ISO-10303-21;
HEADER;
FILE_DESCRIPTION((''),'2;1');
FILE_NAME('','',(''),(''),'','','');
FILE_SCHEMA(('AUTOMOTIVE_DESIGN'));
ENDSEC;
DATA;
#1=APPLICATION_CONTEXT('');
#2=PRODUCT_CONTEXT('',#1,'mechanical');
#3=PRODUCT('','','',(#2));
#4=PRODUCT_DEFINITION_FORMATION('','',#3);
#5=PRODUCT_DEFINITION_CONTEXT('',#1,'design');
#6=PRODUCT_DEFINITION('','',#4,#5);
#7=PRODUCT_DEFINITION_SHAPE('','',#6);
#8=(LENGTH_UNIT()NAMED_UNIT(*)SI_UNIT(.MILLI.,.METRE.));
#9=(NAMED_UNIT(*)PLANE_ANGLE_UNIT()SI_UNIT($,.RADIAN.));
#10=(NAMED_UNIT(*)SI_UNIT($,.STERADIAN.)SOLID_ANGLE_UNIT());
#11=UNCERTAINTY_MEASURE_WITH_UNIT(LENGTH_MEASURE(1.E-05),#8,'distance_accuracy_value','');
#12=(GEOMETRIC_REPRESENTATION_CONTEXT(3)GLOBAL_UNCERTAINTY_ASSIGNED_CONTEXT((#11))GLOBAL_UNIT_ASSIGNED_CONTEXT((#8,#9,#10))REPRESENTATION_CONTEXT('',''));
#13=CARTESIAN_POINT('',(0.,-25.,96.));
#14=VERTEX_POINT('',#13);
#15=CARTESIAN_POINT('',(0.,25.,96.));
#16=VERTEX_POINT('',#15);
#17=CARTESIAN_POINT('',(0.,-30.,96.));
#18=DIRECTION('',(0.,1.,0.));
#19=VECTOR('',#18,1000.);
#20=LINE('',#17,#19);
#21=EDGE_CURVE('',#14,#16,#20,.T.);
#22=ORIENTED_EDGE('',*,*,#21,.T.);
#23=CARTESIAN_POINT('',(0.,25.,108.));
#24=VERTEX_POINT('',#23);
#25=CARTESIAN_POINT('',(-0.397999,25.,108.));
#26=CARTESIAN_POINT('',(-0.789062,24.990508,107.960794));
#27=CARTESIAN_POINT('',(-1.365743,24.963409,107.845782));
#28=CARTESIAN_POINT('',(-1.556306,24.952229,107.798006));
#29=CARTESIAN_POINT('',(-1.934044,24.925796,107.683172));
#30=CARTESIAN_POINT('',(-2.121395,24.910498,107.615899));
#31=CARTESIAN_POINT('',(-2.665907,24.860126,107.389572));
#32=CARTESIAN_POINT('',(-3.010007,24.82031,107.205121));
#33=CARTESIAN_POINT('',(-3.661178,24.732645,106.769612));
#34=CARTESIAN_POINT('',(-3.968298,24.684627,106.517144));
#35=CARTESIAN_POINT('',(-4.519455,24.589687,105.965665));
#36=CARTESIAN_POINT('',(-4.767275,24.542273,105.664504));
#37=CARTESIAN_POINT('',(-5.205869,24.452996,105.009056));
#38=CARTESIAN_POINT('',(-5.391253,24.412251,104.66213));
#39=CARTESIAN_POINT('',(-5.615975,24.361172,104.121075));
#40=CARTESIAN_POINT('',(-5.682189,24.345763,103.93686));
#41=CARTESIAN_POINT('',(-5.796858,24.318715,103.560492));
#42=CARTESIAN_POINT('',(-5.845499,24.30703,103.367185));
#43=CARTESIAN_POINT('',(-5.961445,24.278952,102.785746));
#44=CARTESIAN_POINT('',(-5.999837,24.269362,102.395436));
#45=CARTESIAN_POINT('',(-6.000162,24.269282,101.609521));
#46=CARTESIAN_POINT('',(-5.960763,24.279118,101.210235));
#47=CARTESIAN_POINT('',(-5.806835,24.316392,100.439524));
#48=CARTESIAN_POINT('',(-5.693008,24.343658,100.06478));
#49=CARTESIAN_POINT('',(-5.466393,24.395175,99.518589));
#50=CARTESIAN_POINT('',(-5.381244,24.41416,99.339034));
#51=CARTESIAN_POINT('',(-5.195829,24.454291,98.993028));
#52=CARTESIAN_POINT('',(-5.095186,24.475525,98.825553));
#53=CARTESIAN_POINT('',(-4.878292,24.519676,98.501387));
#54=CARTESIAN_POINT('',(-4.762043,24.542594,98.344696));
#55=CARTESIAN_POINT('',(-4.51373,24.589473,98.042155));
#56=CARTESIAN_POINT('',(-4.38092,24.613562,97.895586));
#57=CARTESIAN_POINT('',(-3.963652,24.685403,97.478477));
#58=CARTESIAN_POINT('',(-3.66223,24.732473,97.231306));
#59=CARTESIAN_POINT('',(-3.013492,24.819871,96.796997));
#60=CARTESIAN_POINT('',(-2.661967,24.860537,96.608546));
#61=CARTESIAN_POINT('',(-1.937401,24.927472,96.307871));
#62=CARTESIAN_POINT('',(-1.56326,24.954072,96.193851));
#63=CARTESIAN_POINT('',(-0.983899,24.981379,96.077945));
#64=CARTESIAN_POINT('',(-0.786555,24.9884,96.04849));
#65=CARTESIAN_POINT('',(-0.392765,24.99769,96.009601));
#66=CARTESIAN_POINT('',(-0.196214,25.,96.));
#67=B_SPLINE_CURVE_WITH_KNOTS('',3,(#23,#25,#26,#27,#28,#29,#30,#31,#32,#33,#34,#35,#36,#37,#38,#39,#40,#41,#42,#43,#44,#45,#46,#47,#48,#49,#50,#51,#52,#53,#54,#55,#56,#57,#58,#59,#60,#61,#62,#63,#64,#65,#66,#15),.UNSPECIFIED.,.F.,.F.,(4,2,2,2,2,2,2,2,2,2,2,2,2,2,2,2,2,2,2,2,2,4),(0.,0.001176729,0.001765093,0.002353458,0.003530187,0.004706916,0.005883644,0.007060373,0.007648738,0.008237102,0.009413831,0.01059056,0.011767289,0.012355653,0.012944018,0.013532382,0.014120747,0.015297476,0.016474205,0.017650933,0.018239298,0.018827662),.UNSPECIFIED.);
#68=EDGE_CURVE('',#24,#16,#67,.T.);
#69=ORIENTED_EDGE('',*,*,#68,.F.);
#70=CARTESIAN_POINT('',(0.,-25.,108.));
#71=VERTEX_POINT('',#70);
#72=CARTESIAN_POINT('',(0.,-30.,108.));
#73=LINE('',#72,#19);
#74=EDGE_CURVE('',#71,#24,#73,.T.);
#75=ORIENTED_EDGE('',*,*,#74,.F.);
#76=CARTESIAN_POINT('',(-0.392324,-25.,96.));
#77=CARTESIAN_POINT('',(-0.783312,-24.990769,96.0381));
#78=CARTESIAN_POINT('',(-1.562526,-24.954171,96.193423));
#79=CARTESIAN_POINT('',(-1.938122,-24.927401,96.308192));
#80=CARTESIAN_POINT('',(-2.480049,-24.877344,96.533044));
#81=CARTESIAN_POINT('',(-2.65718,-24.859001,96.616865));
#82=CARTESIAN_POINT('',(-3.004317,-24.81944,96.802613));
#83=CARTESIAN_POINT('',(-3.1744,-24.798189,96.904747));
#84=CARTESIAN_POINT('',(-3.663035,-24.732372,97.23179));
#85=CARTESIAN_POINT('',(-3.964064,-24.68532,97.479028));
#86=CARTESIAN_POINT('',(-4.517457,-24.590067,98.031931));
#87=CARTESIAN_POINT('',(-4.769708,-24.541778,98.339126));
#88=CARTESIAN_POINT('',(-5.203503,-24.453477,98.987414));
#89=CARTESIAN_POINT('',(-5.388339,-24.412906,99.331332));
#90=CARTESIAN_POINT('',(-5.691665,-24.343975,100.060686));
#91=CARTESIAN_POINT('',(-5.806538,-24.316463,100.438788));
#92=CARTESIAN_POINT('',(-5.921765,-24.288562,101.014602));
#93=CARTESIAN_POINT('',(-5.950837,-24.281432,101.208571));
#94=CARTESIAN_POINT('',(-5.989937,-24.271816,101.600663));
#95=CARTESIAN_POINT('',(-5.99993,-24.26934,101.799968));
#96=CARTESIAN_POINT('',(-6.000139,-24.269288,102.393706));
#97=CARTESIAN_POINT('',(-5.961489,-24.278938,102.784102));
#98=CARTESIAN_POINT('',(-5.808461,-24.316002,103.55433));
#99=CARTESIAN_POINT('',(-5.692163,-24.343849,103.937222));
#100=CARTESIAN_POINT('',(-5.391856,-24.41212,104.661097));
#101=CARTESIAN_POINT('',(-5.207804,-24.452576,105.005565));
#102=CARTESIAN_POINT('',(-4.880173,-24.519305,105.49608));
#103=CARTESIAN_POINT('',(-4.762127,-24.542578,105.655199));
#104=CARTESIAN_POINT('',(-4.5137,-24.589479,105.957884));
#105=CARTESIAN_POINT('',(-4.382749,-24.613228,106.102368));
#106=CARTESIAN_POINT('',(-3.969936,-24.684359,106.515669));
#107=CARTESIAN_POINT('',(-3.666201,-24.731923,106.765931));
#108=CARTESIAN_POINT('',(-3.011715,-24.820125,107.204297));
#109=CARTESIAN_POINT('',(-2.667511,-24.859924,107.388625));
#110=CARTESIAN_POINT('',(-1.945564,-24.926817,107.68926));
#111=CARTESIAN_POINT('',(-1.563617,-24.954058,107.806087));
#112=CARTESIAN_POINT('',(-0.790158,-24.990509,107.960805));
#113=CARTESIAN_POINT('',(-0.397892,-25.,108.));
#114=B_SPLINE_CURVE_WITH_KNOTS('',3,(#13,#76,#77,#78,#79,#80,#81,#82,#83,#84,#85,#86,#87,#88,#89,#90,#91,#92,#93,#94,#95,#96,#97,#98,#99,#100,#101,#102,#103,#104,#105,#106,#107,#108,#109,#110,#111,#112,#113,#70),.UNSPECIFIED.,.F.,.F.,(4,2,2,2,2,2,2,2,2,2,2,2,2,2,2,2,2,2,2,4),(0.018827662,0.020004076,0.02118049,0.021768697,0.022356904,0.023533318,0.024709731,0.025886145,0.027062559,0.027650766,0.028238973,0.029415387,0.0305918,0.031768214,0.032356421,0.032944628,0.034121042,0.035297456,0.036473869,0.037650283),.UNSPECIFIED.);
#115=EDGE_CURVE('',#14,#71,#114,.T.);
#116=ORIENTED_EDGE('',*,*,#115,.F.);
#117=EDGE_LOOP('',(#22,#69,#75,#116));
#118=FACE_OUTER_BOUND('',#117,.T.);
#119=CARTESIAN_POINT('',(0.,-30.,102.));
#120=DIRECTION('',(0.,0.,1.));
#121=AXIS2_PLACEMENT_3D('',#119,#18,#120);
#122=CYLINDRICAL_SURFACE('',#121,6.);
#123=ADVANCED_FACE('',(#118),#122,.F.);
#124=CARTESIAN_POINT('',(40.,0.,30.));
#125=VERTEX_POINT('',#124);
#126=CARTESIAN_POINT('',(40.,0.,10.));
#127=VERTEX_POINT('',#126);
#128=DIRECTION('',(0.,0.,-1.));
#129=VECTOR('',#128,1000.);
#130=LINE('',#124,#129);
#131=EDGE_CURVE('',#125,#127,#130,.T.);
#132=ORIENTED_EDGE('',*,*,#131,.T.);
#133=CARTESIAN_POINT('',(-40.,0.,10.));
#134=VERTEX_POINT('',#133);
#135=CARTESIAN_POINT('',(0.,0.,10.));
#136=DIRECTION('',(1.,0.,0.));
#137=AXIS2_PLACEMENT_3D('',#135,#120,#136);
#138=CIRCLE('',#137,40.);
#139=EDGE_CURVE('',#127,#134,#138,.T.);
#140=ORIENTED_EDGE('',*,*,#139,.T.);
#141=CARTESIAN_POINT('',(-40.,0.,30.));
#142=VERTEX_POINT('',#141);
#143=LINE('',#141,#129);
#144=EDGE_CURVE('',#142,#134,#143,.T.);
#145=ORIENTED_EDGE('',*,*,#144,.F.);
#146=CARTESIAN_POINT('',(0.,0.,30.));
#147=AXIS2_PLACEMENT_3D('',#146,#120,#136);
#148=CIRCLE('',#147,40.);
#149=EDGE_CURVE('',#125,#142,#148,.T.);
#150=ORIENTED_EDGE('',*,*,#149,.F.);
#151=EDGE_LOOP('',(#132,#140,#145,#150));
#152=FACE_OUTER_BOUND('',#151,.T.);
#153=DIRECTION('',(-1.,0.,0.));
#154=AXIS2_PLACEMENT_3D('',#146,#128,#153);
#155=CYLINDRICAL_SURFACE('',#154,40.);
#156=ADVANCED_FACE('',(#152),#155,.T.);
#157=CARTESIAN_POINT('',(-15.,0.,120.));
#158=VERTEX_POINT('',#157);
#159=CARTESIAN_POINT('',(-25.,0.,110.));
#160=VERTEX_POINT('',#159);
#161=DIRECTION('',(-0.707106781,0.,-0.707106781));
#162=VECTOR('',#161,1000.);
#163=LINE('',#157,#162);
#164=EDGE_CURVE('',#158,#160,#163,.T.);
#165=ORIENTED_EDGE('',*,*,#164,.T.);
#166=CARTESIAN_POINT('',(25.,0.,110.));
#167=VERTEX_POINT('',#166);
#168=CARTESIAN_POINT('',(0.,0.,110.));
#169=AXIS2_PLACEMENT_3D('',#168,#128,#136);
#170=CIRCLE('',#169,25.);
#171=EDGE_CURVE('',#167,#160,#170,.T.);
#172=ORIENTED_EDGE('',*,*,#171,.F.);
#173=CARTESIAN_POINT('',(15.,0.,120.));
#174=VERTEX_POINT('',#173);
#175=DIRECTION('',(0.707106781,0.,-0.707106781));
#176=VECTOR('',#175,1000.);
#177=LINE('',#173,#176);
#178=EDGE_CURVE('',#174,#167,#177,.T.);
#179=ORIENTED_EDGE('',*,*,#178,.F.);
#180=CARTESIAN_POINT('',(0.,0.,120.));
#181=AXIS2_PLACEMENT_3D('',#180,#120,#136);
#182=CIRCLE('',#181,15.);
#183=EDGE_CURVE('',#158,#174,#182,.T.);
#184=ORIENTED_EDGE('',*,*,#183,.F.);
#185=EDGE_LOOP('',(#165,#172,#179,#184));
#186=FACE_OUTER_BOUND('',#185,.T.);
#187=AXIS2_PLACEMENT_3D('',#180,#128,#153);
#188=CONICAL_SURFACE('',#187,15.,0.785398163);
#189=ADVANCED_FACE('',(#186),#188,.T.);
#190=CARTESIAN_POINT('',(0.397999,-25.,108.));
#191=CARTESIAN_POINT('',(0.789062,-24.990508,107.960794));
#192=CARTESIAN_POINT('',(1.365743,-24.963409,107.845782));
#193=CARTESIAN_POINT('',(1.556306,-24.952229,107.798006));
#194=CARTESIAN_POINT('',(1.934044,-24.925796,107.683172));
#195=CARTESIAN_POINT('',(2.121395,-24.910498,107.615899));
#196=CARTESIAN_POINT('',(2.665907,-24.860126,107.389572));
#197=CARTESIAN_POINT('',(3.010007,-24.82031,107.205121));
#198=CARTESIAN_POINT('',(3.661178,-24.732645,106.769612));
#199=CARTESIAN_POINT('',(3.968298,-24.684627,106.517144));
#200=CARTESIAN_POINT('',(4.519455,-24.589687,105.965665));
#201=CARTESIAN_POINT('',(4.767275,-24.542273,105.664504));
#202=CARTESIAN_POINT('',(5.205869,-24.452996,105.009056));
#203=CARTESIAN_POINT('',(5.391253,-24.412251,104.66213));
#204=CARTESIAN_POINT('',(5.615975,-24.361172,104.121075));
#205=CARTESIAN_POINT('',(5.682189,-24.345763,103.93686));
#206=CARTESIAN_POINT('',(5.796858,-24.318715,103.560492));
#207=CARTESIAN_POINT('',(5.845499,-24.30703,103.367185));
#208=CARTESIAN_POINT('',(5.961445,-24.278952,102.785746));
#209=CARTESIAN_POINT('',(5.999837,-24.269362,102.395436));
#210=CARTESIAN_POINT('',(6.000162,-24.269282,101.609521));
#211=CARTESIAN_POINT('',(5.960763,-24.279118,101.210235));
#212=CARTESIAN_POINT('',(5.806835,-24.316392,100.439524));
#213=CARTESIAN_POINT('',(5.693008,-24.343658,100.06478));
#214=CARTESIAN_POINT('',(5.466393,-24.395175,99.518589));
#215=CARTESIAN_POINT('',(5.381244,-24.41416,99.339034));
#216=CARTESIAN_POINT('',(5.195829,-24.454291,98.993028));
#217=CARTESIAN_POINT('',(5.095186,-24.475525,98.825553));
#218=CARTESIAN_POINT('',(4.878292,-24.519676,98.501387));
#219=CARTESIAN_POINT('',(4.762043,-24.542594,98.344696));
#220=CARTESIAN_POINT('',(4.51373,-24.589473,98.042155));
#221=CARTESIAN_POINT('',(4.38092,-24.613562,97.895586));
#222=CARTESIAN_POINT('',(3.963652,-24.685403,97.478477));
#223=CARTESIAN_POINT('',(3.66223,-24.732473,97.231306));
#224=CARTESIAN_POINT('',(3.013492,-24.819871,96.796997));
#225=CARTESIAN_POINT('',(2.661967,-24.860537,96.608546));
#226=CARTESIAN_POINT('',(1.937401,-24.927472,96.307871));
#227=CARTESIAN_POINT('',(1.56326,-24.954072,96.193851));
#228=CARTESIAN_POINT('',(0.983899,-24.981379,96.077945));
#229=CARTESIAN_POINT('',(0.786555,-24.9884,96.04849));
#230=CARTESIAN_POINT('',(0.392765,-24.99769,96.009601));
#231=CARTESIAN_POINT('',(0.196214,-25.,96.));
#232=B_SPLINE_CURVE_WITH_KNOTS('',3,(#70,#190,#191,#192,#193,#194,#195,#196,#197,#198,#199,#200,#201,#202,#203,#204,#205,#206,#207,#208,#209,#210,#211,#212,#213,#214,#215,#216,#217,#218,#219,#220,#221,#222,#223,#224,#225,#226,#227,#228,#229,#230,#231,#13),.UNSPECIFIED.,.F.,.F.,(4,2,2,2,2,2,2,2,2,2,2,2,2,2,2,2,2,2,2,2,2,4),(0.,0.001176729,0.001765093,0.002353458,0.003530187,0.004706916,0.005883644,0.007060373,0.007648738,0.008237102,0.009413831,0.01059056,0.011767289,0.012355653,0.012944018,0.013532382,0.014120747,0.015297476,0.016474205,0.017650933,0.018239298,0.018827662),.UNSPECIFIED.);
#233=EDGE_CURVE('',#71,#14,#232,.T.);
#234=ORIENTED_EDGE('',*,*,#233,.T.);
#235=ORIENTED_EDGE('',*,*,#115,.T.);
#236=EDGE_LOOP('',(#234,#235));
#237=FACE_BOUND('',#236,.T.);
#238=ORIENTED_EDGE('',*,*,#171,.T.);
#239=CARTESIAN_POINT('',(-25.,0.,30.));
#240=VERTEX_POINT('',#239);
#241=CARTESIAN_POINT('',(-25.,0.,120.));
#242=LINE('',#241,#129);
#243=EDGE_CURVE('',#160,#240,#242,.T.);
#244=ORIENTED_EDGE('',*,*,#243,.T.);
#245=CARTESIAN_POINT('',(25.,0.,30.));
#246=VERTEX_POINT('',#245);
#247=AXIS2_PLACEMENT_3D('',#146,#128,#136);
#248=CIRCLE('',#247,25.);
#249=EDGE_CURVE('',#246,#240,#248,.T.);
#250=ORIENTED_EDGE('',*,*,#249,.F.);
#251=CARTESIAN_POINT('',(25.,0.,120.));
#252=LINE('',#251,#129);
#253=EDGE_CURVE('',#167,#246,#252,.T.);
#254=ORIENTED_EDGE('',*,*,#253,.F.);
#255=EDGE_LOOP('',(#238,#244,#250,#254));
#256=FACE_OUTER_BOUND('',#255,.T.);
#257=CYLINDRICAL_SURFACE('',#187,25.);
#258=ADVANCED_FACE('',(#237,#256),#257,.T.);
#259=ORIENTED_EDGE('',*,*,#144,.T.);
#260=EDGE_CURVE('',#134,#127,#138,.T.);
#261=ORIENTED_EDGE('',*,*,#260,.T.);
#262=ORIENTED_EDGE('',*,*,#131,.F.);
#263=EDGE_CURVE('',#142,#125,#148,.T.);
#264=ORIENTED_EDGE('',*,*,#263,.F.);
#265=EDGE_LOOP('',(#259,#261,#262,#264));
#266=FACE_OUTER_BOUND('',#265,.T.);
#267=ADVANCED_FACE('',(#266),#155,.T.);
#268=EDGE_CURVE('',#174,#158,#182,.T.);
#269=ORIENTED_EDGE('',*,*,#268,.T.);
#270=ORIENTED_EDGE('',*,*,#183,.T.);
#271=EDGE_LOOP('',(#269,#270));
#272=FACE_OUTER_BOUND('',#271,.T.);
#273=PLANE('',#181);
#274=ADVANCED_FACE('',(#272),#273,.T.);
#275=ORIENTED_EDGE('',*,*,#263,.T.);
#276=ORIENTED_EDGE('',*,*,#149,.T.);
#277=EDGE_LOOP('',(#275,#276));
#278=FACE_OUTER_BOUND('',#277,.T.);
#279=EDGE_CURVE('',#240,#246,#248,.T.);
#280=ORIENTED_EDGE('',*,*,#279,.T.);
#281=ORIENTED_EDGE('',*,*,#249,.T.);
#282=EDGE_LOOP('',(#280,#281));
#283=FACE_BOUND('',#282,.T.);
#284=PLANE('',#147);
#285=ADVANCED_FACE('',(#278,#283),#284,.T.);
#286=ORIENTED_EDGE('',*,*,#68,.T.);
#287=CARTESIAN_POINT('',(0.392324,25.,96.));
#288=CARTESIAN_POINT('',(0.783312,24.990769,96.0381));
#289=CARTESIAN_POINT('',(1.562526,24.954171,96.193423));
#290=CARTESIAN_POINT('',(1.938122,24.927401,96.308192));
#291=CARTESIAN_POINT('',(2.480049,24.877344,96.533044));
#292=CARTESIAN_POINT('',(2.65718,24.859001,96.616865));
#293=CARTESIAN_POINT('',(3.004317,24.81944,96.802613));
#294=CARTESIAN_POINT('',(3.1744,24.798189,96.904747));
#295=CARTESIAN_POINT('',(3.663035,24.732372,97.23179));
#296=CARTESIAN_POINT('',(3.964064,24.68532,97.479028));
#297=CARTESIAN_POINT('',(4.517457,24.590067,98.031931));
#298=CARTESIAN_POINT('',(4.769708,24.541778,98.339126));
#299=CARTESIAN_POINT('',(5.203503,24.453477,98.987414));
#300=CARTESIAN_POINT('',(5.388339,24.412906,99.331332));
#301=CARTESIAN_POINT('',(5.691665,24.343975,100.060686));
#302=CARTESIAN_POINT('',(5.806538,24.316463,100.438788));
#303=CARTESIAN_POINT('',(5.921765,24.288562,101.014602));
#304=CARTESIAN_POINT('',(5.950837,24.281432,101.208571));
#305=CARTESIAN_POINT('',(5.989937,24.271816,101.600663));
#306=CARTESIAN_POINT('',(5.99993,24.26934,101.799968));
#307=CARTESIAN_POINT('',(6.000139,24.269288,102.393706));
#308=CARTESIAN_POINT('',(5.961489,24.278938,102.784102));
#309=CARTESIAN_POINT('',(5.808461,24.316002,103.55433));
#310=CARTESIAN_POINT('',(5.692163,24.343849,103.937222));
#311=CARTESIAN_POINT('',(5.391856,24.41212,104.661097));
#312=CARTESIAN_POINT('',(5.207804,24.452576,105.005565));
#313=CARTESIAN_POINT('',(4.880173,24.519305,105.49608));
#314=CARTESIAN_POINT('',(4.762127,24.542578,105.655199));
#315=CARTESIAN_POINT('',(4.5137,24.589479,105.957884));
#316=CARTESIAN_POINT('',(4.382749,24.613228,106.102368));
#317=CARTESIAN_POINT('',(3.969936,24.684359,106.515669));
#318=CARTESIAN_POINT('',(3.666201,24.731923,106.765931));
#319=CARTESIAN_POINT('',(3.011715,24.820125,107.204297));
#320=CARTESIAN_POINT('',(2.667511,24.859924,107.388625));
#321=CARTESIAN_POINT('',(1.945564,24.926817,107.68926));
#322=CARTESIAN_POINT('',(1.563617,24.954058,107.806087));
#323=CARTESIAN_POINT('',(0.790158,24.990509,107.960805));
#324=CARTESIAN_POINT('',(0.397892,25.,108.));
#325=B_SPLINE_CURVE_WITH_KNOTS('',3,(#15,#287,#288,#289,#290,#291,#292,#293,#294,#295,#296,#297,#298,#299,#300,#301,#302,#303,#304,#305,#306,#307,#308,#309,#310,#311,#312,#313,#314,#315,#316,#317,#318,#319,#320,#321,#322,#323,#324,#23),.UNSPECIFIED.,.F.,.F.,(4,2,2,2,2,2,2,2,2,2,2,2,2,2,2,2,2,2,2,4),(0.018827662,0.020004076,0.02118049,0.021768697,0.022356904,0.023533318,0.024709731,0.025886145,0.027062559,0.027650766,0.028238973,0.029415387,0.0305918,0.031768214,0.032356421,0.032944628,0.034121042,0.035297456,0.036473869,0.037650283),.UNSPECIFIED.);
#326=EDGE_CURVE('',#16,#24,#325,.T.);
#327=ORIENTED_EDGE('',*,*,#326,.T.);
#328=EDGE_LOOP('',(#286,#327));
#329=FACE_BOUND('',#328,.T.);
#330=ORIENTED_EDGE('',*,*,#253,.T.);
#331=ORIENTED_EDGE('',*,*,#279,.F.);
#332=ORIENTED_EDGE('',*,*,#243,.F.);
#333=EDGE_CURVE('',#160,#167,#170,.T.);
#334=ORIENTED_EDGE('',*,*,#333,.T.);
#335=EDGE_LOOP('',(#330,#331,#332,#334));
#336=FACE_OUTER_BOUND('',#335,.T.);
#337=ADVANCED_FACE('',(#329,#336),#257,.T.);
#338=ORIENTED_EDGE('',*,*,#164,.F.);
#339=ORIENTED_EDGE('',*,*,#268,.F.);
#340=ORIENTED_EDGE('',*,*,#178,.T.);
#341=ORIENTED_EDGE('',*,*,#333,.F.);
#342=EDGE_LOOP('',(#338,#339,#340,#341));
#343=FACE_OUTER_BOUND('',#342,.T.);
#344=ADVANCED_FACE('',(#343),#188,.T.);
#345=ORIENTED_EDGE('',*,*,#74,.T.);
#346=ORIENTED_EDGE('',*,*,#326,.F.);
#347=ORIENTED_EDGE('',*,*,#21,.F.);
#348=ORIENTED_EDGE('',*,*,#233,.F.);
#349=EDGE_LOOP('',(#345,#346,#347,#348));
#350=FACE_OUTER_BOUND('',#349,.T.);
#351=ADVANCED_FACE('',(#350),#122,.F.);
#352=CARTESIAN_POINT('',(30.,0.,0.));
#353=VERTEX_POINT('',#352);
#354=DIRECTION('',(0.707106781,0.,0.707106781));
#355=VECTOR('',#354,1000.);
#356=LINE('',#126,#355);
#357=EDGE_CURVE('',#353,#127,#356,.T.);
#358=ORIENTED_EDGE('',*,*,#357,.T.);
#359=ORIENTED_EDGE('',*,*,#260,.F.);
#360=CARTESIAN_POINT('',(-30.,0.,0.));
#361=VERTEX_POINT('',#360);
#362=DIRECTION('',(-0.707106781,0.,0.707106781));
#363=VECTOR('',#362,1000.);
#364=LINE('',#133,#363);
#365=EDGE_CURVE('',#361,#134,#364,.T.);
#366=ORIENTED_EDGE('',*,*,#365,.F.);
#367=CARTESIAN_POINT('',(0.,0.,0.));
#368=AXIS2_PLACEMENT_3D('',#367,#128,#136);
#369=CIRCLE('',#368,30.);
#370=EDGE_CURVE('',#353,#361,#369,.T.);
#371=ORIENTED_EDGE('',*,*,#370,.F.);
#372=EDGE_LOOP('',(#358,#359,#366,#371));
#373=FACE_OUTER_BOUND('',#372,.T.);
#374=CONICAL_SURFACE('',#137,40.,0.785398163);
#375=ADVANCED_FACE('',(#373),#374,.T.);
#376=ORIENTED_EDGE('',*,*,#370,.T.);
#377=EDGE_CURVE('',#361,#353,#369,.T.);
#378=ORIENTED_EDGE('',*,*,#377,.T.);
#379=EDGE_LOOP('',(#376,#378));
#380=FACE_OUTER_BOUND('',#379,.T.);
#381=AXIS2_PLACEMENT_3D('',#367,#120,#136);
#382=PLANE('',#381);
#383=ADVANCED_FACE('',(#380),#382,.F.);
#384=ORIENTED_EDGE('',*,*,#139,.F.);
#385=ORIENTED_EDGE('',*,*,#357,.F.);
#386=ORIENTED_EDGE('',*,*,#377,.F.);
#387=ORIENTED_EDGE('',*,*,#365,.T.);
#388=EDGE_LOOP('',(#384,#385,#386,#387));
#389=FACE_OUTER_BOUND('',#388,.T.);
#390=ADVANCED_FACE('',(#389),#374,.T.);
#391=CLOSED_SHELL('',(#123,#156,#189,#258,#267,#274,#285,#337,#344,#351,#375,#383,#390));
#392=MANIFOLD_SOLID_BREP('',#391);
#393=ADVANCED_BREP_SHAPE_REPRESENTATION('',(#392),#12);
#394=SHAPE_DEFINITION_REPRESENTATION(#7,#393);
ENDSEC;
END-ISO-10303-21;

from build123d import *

# Parameters (mm, degrees)
HEAD_AND_SHANK_PROFILE_80_50_R   = 40
HEAD_AND_SHANK_PROFILE_80_50_R_2 = 25
HEAD_80_DEPTH                    = 30
SKETCH1_3_R                      = 25
SHANK_50_DEPTH                   = 120
HEAD_CHAMFER_10X45_SIZE          = 10
SHANK_END_CHAMFER_10X45_SIZE     = 10
CROSS_HOLE_PROFILE_R             = 6
CROSS_HOLE_12_DEPTH              = 30


with BuildPart() as part:
    # Head and Shank Profile _80-_50 → Head _80 (new body)
    # profile 1 of 2: a face of its own
    with BuildSketch(Plane.XY):
        Circle(HEAD_AND_SHANK_PROFILE_80_50_R)
        Circle(HEAD_AND_SHANK_PROFILE_80_50_R_2, mode=Mode.SUBTRACT)
    # profile 2 of 2: a face of its own
    with BuildSketch(Plane.XY):
        Circle(HEAD_AND_SHANK_PROFILE_80_50_R_2)
    extrude(amount=HEAD_80_DEPTH)

    # Sketch1_3 → Shank _50 (add)
    with BuildSketch(Plane.XY):
        with Locations(Location((0, 0, 0), (0, 0, 180))):
            Circle(SKETCH1_3_R)
    extrude(amount=SHANK_50_DEPTH)

    # Head Chamfer 10x45
    head_chamfer_10x45_edges = [part.edges().sort_by_distance(p)[0] for p in [
        (-40, 0, 0),
    ]]
    chamfer(head_chamfer_10x45_edges, length=HEAD_CHAMFER_10X45_SIZE)

    # Shank End Chamfer 10x45
    shank_end_chamfer_10x45_edges = [part.edges().sort_by_distance(p)[0] for p in [
        (25, 0, 120),
    ]]
    chamfer(shank_end_chamfer_10x45_edges, length=SHANK_END_CHAMFER_10X45_SIZE)

    # Cross Hole Profile → Cross Hole _12 (cut, symmetric)
    with BuildSketch(Plane(origin=(0, 0, 0), x_dir=(1, 0, 0), z_dir=(0, 1, 0))):
        with Locations(Location((0, -102, 0), (0, 0, 270))):
            Circle(CROSS_HOLE_PROFILE_R)
    extrude(amount=CROSS_HOLE_12_DEPTH, both=True, mode=Mode.SUBTRACT)


solid = part.part
